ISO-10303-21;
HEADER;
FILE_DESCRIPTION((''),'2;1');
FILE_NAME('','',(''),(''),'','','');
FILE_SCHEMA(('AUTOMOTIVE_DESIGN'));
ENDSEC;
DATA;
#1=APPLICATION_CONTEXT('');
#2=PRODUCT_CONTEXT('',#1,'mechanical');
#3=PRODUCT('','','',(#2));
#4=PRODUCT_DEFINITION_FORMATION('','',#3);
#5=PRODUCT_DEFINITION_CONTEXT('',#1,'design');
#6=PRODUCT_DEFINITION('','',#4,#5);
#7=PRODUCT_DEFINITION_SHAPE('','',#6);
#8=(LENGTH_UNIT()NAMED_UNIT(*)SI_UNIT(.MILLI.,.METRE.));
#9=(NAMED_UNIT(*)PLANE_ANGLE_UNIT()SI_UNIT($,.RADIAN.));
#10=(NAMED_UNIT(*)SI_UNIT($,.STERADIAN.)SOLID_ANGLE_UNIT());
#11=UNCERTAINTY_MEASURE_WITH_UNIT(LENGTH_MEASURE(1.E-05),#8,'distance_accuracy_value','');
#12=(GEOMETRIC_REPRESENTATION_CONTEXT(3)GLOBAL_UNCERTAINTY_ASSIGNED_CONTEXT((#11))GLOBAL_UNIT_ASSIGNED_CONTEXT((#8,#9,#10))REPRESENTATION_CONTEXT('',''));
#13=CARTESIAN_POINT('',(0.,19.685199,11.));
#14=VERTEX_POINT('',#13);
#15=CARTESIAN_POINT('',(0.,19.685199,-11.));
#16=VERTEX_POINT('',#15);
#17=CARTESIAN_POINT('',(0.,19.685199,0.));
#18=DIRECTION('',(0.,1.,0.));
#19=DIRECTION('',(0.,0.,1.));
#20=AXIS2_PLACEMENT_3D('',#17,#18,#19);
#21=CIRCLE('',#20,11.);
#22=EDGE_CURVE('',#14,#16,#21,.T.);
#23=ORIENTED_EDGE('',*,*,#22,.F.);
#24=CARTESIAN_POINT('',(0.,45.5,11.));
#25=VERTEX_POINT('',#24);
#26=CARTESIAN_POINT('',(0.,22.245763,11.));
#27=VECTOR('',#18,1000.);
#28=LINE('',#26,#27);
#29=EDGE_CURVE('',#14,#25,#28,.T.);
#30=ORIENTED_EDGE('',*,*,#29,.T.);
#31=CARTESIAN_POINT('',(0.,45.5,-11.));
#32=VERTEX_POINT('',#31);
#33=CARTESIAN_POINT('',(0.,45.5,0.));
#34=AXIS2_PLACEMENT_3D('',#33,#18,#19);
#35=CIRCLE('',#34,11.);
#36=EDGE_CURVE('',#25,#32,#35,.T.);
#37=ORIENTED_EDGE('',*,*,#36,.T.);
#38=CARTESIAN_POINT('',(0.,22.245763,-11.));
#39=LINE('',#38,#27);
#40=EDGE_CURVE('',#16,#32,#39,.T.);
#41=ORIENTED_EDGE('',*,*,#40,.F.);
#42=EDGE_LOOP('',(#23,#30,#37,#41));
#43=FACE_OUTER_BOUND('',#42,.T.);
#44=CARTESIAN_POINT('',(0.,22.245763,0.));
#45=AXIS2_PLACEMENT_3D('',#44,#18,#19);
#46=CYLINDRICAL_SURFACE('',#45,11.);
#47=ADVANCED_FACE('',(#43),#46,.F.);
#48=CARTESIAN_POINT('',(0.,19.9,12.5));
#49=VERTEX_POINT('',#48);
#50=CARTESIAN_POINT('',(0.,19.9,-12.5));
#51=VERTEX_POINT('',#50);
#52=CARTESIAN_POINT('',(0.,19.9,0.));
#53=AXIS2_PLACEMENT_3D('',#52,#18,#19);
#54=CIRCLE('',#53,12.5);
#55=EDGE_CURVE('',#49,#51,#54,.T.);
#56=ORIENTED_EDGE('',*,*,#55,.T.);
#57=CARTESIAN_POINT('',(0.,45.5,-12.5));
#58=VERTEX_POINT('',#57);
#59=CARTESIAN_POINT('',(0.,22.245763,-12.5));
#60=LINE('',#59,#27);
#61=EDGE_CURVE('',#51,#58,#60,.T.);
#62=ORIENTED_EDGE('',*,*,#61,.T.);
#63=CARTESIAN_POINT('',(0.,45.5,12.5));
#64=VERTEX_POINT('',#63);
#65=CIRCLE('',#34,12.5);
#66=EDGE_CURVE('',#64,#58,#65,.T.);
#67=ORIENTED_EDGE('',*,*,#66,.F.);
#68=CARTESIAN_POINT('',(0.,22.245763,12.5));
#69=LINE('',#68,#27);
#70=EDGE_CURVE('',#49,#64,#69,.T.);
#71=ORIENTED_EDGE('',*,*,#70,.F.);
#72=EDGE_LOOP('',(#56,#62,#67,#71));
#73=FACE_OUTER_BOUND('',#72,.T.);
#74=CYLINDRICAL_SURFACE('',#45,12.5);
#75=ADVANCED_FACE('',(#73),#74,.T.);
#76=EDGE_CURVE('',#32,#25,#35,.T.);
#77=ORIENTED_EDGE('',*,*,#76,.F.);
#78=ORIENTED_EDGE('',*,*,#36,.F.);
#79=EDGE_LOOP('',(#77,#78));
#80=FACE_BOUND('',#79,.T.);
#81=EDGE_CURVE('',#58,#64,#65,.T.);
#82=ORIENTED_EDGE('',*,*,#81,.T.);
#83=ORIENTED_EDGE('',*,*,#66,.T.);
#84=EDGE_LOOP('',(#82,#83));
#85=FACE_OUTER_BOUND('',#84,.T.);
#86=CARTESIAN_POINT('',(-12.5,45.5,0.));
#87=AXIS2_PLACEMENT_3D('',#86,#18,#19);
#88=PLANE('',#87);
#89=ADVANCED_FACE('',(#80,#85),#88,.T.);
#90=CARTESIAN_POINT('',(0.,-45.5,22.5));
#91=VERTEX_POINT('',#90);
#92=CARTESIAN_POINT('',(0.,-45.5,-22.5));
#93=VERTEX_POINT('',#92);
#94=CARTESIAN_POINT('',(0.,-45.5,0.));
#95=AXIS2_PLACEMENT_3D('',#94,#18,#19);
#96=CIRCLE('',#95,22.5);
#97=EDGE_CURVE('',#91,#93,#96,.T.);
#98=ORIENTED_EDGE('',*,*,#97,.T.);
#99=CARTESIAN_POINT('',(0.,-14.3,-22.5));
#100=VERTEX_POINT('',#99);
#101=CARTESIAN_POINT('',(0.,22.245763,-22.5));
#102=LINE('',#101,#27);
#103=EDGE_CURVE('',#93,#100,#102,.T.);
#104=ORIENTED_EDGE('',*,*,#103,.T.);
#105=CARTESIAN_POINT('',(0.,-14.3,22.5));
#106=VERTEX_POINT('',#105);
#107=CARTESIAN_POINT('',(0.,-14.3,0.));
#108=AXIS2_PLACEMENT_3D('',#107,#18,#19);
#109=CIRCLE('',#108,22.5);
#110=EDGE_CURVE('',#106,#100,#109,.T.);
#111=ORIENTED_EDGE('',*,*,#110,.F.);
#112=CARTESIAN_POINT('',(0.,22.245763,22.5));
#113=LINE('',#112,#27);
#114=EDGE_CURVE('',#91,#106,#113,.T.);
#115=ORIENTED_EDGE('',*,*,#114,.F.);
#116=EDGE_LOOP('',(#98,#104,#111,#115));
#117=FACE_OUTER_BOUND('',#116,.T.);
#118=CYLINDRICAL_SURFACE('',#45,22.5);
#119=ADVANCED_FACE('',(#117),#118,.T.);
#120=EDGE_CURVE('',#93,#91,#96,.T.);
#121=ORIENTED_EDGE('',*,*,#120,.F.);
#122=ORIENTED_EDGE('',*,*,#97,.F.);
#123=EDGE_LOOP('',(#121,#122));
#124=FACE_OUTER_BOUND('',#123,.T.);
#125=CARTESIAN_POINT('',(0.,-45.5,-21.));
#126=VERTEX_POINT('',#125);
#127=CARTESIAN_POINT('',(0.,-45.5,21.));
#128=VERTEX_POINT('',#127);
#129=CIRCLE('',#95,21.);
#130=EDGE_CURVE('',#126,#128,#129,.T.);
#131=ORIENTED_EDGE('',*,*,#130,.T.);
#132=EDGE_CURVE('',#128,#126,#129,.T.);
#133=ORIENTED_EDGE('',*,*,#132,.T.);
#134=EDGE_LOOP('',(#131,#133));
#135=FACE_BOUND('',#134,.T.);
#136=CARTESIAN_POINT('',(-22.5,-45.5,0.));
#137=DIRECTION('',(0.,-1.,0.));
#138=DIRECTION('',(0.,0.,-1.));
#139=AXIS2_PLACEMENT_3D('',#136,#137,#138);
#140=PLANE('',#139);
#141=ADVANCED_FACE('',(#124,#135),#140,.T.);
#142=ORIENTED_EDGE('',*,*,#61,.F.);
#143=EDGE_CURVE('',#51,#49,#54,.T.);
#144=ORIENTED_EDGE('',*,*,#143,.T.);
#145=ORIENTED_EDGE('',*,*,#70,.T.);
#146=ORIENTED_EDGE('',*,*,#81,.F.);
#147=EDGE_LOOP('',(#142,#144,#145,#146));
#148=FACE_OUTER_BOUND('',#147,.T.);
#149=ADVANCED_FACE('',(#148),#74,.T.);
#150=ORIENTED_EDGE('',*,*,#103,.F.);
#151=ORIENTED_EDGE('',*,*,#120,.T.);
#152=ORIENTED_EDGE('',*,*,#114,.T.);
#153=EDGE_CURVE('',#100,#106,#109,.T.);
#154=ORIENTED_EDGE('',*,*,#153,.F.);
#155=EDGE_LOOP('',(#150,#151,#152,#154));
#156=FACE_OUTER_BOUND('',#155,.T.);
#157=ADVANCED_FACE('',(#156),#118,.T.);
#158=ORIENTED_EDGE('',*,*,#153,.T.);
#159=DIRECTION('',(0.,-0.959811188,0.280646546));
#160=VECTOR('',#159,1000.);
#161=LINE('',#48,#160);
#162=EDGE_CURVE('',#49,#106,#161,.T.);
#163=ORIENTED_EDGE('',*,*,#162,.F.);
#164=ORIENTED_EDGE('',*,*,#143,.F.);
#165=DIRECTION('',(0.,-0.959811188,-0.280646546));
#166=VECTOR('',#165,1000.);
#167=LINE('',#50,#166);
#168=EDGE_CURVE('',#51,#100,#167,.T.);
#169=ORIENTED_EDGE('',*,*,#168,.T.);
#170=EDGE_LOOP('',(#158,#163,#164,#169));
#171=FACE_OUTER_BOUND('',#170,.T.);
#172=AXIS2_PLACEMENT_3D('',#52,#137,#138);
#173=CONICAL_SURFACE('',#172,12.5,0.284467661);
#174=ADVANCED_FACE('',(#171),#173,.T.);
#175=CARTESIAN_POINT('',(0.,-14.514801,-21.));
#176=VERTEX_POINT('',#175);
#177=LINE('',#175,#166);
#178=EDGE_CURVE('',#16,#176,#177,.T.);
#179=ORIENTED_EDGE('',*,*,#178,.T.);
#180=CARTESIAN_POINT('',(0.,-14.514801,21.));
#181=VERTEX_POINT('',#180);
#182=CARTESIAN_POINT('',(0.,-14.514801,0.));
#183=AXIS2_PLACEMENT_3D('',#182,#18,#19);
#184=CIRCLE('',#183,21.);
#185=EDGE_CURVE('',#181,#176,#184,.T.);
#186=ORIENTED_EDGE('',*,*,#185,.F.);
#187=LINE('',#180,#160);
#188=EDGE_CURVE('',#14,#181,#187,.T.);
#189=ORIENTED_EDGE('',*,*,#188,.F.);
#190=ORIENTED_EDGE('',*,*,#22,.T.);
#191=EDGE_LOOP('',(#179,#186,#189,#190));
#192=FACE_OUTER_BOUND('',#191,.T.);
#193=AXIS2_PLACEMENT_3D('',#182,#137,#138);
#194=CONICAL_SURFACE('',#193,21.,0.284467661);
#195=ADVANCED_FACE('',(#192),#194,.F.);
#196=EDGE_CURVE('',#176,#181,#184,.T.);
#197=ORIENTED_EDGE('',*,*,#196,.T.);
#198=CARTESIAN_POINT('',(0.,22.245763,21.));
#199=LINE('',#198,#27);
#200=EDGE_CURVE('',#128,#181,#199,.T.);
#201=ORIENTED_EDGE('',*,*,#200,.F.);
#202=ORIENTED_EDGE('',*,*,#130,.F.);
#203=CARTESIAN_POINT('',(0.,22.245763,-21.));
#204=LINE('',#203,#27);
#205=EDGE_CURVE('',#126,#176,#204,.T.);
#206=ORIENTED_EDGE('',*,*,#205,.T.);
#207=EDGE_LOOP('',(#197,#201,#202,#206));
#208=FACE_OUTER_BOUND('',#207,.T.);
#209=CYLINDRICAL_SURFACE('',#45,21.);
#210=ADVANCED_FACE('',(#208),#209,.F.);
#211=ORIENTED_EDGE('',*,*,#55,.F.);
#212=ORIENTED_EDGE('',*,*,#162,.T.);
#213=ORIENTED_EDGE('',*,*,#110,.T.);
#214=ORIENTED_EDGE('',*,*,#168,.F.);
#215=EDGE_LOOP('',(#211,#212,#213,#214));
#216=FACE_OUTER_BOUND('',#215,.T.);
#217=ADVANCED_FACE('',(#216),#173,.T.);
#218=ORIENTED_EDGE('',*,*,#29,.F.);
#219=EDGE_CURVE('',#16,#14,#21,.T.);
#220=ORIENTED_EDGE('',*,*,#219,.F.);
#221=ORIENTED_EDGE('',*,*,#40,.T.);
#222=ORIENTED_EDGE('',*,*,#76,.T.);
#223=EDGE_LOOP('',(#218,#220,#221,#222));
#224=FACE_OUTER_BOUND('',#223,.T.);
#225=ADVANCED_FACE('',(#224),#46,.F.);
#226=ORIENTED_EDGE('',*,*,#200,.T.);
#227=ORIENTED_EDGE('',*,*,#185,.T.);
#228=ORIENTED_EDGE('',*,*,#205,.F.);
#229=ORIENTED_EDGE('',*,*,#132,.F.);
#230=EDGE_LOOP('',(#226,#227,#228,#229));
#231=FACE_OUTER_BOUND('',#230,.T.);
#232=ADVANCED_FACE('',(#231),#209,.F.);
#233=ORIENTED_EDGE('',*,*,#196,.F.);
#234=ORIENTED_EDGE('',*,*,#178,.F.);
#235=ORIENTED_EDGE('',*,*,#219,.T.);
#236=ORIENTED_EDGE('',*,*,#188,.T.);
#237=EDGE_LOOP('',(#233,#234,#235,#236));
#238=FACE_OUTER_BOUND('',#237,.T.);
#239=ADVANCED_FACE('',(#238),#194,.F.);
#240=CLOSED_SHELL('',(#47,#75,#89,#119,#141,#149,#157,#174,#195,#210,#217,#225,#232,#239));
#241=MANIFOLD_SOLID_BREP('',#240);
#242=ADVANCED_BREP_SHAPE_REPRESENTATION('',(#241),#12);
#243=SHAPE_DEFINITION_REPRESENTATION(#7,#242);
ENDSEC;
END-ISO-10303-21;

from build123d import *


with BuildPart() as part:
    # Sketch 1 → Revolve 1 (revolve)
    with BuildSketch(Plane.XY, mode=Mode.PRIVATE) as revolve_1_sk:
        Polygon((-12.5, 45.5), (-12.5, 19.9), (-22.5, -14.3), (-22.5, -45.5), (-21, -45.5), (-21, -14.514801212), (-11, 19.685198788), (-11, 45.5), align=None)
    revolve(revolve_1_sk.sketch.rotate(Axis((0, 22.245762712, 0), (0, -1, 0)), 270), axis=Axis((0, 22.245762712, 0), (0, -1, 0)))


solid = part.part
